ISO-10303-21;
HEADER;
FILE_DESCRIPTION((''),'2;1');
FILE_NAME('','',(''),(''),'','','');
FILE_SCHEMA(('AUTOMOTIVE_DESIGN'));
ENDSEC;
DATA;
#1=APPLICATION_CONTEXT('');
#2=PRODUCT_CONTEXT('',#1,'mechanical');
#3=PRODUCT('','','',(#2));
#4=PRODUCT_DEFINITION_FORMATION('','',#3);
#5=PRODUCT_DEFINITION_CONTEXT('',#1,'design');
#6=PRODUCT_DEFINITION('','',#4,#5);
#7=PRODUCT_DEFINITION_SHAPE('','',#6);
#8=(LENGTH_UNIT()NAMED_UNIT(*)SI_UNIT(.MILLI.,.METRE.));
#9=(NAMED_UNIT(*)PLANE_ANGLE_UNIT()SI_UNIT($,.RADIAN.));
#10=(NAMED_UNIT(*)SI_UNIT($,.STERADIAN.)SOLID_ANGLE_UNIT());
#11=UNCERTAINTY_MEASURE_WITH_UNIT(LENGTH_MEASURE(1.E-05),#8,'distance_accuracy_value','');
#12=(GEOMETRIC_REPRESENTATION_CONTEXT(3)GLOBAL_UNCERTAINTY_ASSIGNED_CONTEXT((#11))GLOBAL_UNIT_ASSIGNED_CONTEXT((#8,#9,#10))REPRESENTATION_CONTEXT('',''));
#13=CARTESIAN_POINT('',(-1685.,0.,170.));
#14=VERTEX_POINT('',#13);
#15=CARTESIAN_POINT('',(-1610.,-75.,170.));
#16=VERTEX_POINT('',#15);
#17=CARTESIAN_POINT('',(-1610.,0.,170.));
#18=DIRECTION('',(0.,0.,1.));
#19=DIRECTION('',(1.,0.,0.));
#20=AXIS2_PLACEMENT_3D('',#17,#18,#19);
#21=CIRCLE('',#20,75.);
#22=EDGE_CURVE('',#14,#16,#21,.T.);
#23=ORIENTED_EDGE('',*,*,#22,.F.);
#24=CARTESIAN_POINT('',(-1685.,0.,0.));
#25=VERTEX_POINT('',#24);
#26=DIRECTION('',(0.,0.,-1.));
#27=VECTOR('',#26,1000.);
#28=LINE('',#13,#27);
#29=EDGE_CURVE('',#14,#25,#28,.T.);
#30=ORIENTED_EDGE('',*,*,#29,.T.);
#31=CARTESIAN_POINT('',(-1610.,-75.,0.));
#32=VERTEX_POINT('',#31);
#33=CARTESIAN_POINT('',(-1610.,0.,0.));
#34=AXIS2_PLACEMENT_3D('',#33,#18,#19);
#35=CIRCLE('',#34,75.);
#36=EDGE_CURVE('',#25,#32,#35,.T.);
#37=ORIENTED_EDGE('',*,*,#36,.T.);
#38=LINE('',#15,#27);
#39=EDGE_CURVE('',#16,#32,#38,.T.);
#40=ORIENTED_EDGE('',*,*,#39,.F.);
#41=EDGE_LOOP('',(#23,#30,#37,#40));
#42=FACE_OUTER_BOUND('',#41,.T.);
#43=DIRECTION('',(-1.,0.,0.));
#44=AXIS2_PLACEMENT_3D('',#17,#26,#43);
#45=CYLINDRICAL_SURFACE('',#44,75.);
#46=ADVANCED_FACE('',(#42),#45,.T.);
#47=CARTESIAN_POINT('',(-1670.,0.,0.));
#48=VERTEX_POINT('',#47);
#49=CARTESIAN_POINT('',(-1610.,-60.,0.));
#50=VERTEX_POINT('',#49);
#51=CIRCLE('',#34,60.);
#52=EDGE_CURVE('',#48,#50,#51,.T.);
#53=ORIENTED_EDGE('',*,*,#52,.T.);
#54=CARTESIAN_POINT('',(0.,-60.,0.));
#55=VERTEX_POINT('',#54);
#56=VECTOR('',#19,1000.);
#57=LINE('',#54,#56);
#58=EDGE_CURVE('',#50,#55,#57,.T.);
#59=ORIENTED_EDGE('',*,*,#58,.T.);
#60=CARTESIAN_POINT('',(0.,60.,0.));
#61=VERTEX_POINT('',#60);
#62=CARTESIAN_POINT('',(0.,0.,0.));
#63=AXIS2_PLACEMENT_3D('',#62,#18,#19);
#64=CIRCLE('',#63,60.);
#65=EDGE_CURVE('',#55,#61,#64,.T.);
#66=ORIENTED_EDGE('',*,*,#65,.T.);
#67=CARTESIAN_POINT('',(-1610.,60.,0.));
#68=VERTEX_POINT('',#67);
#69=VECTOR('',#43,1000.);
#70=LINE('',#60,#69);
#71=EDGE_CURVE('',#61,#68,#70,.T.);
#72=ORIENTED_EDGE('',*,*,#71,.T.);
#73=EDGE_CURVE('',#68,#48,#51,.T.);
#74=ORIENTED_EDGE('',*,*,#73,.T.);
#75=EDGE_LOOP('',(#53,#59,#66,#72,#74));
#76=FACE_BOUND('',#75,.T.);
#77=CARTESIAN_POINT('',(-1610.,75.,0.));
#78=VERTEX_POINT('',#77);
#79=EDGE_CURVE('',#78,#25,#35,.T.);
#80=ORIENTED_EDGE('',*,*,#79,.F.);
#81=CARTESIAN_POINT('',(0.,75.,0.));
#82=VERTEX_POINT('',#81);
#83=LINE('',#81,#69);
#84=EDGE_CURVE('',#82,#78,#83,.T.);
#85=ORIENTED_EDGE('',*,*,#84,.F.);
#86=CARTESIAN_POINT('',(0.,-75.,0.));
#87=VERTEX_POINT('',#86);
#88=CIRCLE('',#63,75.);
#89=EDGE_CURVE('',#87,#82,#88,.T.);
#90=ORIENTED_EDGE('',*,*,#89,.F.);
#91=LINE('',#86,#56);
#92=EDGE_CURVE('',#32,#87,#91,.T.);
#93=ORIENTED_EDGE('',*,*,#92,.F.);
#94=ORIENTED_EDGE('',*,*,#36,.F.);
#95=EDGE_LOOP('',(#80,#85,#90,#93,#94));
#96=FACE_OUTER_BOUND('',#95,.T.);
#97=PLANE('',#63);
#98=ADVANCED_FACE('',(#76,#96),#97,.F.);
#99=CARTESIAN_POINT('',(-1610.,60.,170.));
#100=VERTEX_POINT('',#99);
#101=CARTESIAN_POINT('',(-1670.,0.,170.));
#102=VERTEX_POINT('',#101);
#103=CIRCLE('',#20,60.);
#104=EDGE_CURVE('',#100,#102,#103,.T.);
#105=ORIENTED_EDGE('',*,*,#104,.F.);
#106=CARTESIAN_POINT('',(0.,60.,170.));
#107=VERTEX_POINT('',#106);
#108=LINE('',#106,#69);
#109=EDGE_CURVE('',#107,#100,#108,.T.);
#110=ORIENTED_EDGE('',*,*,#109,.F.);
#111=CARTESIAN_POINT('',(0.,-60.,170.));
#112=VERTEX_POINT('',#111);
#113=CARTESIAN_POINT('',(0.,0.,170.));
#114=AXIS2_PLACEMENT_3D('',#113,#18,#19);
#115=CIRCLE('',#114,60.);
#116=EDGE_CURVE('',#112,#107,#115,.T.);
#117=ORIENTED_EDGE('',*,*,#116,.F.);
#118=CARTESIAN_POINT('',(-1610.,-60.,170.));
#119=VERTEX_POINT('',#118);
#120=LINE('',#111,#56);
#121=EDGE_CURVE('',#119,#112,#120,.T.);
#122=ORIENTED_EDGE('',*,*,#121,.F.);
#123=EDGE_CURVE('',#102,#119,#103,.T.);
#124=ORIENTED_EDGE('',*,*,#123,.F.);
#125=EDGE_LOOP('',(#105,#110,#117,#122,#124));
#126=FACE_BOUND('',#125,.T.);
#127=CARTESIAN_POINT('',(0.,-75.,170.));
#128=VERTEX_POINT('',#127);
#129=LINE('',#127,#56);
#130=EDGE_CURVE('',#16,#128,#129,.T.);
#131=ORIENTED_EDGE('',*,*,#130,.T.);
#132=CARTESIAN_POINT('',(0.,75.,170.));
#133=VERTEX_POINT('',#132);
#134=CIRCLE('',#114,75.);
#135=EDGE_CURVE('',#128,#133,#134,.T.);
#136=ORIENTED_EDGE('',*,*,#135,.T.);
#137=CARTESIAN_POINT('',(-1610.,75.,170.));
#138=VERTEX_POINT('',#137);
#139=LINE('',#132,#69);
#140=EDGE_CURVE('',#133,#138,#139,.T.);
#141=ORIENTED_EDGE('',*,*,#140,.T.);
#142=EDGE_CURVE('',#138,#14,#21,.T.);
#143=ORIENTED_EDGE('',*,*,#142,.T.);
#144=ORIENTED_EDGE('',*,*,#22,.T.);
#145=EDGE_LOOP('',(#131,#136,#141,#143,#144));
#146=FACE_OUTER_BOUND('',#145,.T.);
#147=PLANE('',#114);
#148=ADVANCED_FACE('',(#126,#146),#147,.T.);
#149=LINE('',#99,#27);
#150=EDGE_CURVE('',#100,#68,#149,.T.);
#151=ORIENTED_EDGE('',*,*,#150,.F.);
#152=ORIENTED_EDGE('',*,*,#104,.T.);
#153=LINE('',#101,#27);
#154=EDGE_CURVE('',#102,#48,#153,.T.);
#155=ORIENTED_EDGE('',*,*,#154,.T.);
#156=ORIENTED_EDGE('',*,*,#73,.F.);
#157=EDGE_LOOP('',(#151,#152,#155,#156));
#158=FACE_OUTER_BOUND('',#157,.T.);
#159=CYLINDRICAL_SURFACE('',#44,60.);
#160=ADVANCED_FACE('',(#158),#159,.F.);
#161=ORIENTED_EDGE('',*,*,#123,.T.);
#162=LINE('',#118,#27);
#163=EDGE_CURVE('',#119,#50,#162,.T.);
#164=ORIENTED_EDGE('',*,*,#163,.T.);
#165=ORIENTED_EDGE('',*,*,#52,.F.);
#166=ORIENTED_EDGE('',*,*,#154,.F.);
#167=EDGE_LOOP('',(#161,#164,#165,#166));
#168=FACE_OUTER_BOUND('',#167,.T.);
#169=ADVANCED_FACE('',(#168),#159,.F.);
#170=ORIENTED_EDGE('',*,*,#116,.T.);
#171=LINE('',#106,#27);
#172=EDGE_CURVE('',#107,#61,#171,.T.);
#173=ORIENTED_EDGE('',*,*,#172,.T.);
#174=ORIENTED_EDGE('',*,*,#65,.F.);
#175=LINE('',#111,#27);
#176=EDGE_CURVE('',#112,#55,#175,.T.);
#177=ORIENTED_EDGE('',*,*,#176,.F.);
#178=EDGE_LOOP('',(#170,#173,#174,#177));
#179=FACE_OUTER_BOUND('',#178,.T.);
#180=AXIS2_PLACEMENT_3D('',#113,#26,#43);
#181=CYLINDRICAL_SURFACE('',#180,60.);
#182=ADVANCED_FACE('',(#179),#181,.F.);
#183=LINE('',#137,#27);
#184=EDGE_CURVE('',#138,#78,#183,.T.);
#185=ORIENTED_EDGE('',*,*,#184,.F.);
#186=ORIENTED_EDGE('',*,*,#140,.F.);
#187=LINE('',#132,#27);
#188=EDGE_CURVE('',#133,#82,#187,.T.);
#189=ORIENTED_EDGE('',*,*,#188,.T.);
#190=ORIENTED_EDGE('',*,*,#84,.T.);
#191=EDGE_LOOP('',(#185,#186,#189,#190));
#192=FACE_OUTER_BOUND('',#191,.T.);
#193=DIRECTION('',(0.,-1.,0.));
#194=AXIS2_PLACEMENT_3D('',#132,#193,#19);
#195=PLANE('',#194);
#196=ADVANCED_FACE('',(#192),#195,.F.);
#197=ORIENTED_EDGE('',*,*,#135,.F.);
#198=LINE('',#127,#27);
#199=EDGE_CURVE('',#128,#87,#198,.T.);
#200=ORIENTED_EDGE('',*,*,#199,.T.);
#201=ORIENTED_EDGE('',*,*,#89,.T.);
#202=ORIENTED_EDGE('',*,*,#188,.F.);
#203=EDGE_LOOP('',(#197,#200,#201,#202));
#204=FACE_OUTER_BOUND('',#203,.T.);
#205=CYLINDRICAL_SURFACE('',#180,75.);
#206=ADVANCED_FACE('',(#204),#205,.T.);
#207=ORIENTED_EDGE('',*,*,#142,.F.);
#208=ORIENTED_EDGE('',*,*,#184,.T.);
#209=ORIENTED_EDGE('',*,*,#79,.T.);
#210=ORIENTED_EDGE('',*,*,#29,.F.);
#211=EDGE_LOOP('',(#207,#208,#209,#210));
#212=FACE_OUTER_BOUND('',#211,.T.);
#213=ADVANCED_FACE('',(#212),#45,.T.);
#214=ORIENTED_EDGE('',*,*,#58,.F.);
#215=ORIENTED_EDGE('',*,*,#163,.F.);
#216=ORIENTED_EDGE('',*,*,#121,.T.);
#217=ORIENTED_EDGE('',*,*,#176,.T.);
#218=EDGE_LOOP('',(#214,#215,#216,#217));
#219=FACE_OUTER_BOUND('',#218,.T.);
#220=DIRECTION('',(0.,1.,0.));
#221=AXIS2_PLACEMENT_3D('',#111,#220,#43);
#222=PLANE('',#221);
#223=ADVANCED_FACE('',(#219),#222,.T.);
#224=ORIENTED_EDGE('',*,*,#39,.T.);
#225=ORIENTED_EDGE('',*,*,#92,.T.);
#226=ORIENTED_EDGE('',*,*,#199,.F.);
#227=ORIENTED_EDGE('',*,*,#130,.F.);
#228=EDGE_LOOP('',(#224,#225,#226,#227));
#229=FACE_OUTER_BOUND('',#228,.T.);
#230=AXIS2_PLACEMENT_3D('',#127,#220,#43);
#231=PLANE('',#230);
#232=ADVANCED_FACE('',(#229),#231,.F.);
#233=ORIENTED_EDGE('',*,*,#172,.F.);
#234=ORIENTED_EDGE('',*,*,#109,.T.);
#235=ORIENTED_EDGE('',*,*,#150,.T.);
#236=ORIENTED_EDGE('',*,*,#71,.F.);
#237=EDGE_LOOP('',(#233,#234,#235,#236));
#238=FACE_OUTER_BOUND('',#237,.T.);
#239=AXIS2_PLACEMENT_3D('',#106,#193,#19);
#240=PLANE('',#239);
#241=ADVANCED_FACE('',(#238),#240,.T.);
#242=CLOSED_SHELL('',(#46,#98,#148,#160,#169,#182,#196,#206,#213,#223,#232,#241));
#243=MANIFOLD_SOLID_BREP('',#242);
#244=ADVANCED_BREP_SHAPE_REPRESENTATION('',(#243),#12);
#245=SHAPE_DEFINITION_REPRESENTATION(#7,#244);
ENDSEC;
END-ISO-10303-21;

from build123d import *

# Parameters (mm, degrees)
EXTRUDE_1_DEPTH = 170


with BuildPart() as part:
    # 草图1 → 凸台-拉伸1 (new body)
    with BuildSketch(Plane.XY):
        with BuildLine():
            Line((0, 75), (-1610, 75))
            ThreePointArc((-1610, 75), (-1685, 0), (-1610, -75))
            Line((-1610, -75), (0, -75))
            ThreePointArc((0, -75), (75, 0), (0, 75))
        make_face()
        with BuildLine():
            Line((0, 60), (-1610, 60))
            ThreePointArc((-1610, 60), (-1670, 0), (-1610, -60))
            Line((-1610, -60), (0, -60))
            ThreePointArc((0, -60), (60, 0), (0, 60))
        make_face(mode=Mode.SUBTRACT)
    extrude(amount=EXTRUDE_1_DEPTH)


solid = part.part
